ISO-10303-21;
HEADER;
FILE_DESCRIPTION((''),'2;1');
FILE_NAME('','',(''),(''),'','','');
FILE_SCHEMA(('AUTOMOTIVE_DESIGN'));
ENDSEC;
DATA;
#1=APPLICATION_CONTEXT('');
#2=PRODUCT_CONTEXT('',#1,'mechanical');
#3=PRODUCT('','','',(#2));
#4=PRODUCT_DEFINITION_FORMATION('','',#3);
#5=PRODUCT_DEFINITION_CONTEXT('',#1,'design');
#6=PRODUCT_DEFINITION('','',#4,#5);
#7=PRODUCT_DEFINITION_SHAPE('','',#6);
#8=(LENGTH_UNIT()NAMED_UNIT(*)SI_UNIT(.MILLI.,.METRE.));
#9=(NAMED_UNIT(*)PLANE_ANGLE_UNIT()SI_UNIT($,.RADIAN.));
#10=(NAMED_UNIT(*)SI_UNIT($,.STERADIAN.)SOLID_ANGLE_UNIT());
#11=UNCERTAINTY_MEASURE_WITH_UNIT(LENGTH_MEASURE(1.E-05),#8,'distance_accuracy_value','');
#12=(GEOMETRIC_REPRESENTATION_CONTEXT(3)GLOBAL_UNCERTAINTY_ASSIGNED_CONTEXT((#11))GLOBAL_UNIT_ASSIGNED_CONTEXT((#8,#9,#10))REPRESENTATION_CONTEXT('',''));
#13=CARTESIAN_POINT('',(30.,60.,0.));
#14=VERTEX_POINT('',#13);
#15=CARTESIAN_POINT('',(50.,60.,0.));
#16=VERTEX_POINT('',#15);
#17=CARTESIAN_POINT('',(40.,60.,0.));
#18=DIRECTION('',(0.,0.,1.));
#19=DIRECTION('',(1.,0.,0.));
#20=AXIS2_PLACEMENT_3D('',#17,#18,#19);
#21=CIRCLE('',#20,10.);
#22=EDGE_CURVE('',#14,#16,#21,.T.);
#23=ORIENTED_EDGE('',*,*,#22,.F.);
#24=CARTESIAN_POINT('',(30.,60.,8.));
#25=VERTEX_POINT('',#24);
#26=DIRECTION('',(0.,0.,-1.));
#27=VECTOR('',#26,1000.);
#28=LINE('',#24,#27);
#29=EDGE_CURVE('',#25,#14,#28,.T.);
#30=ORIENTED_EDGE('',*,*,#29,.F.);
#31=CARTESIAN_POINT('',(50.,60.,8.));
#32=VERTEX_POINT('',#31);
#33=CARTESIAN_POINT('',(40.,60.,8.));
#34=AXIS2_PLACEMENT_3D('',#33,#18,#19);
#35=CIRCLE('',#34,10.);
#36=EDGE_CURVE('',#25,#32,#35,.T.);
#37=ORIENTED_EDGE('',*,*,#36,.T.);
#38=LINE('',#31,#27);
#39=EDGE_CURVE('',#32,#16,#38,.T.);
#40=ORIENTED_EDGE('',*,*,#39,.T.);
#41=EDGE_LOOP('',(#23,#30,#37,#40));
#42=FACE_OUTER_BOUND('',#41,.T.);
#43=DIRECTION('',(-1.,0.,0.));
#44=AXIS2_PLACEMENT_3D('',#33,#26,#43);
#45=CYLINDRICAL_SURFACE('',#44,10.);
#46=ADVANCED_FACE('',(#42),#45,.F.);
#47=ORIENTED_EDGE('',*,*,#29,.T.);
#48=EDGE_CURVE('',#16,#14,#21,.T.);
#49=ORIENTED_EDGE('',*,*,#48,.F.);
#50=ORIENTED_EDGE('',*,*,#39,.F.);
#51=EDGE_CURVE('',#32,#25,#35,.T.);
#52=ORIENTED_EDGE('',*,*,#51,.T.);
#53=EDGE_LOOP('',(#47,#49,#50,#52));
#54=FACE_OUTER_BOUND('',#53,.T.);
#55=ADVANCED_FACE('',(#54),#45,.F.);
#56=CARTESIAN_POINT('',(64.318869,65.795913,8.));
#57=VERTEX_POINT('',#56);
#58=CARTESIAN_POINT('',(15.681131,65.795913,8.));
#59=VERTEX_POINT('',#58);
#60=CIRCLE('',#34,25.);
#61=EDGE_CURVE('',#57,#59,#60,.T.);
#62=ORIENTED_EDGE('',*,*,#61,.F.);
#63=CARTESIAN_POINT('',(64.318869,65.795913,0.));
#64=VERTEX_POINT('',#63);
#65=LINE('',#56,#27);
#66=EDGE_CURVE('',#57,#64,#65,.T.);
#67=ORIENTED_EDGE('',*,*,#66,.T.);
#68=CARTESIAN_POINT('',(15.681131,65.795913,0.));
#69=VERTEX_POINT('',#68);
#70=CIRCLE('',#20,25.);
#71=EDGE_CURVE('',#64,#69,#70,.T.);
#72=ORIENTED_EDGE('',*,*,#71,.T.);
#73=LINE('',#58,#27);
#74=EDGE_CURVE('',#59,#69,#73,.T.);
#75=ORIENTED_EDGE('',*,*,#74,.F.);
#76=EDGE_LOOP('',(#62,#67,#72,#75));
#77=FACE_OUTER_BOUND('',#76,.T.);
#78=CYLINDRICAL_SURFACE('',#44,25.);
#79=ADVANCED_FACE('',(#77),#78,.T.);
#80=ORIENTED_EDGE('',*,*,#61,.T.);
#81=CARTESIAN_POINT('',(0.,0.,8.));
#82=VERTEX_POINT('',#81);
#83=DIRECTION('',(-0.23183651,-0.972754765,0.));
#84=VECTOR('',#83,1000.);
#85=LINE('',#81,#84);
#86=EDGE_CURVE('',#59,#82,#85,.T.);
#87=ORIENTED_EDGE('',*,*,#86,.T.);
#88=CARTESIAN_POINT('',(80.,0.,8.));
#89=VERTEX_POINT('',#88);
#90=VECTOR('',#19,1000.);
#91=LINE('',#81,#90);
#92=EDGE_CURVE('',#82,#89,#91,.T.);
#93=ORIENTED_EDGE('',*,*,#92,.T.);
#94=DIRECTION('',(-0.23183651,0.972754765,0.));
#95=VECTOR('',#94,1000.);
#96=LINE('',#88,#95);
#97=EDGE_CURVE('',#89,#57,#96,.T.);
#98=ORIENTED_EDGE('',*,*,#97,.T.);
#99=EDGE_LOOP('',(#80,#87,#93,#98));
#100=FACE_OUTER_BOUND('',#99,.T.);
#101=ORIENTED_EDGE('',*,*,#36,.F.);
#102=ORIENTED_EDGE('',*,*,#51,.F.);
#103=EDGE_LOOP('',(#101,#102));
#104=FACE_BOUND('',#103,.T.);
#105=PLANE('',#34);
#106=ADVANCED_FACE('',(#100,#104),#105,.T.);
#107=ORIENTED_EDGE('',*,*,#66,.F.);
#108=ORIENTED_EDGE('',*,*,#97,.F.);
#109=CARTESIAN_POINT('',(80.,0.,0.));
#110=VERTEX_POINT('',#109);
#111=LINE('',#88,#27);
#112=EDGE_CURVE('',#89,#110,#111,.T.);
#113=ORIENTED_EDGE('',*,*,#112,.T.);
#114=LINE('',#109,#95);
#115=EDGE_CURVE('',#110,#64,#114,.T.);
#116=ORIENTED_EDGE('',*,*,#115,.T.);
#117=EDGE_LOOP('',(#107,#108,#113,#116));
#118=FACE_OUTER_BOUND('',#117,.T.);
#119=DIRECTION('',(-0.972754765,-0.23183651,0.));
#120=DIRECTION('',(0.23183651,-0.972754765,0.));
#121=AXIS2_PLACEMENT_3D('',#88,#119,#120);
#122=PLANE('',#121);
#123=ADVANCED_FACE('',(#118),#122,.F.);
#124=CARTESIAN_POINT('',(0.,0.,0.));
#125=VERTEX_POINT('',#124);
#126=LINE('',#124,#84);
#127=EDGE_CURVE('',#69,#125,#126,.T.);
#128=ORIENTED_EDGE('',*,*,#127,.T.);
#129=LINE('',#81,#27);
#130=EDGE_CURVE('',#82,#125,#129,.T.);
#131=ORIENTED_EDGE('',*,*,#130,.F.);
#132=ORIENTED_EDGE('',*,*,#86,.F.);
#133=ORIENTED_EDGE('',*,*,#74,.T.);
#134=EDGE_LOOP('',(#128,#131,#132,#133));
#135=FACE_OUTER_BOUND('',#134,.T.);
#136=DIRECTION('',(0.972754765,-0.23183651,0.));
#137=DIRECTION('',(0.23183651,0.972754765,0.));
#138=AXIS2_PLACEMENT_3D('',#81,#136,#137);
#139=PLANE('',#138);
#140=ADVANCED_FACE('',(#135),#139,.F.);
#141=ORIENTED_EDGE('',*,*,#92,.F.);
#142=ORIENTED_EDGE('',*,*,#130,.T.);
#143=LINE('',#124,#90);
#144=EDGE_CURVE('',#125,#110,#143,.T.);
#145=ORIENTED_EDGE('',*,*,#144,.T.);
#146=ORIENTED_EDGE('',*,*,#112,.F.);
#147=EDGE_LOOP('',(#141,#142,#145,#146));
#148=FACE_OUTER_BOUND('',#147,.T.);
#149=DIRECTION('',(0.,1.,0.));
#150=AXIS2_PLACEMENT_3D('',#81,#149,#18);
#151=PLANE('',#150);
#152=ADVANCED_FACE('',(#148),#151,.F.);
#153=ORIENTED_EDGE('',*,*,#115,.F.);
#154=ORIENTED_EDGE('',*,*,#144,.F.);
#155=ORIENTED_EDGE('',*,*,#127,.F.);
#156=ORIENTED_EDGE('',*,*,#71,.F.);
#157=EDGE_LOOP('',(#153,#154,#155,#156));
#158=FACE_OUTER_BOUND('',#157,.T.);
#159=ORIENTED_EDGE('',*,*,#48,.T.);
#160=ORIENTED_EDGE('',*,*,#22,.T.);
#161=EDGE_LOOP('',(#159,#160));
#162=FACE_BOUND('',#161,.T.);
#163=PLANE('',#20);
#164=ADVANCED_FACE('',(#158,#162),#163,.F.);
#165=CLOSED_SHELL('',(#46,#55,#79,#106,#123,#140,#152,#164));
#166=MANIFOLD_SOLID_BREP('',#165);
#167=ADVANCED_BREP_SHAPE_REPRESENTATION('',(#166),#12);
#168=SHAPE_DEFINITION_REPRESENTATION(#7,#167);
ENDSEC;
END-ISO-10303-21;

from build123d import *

# Parameters (mm, degrees)
SKETCH_1_R      = 10
EXTRUDE_1_DEPTH = 8


with BuildPart() as part:
    # 草图1 → 凸台-拉伸1 (new body)
    with BuildSketch(Plane.XY):
        with BuildLine():
            Line((0, 0), (80, 0))
            Line((80, 0), (64.318869123, 65.795912749))
            ThreePointArc((64.318869123, 65.795912749), (40, 85), (15.681130877, 65.795912749))
            Line((15.681130877, 65.795912749), (0, 0))
        make_face()
        with Locations((40, 60)):
            Circle(SKETCH_1_R, mode=Mode.SUBTRACT)
    extrude(amount=EXTRUDE_1_DEPTH)


solid = part.part
